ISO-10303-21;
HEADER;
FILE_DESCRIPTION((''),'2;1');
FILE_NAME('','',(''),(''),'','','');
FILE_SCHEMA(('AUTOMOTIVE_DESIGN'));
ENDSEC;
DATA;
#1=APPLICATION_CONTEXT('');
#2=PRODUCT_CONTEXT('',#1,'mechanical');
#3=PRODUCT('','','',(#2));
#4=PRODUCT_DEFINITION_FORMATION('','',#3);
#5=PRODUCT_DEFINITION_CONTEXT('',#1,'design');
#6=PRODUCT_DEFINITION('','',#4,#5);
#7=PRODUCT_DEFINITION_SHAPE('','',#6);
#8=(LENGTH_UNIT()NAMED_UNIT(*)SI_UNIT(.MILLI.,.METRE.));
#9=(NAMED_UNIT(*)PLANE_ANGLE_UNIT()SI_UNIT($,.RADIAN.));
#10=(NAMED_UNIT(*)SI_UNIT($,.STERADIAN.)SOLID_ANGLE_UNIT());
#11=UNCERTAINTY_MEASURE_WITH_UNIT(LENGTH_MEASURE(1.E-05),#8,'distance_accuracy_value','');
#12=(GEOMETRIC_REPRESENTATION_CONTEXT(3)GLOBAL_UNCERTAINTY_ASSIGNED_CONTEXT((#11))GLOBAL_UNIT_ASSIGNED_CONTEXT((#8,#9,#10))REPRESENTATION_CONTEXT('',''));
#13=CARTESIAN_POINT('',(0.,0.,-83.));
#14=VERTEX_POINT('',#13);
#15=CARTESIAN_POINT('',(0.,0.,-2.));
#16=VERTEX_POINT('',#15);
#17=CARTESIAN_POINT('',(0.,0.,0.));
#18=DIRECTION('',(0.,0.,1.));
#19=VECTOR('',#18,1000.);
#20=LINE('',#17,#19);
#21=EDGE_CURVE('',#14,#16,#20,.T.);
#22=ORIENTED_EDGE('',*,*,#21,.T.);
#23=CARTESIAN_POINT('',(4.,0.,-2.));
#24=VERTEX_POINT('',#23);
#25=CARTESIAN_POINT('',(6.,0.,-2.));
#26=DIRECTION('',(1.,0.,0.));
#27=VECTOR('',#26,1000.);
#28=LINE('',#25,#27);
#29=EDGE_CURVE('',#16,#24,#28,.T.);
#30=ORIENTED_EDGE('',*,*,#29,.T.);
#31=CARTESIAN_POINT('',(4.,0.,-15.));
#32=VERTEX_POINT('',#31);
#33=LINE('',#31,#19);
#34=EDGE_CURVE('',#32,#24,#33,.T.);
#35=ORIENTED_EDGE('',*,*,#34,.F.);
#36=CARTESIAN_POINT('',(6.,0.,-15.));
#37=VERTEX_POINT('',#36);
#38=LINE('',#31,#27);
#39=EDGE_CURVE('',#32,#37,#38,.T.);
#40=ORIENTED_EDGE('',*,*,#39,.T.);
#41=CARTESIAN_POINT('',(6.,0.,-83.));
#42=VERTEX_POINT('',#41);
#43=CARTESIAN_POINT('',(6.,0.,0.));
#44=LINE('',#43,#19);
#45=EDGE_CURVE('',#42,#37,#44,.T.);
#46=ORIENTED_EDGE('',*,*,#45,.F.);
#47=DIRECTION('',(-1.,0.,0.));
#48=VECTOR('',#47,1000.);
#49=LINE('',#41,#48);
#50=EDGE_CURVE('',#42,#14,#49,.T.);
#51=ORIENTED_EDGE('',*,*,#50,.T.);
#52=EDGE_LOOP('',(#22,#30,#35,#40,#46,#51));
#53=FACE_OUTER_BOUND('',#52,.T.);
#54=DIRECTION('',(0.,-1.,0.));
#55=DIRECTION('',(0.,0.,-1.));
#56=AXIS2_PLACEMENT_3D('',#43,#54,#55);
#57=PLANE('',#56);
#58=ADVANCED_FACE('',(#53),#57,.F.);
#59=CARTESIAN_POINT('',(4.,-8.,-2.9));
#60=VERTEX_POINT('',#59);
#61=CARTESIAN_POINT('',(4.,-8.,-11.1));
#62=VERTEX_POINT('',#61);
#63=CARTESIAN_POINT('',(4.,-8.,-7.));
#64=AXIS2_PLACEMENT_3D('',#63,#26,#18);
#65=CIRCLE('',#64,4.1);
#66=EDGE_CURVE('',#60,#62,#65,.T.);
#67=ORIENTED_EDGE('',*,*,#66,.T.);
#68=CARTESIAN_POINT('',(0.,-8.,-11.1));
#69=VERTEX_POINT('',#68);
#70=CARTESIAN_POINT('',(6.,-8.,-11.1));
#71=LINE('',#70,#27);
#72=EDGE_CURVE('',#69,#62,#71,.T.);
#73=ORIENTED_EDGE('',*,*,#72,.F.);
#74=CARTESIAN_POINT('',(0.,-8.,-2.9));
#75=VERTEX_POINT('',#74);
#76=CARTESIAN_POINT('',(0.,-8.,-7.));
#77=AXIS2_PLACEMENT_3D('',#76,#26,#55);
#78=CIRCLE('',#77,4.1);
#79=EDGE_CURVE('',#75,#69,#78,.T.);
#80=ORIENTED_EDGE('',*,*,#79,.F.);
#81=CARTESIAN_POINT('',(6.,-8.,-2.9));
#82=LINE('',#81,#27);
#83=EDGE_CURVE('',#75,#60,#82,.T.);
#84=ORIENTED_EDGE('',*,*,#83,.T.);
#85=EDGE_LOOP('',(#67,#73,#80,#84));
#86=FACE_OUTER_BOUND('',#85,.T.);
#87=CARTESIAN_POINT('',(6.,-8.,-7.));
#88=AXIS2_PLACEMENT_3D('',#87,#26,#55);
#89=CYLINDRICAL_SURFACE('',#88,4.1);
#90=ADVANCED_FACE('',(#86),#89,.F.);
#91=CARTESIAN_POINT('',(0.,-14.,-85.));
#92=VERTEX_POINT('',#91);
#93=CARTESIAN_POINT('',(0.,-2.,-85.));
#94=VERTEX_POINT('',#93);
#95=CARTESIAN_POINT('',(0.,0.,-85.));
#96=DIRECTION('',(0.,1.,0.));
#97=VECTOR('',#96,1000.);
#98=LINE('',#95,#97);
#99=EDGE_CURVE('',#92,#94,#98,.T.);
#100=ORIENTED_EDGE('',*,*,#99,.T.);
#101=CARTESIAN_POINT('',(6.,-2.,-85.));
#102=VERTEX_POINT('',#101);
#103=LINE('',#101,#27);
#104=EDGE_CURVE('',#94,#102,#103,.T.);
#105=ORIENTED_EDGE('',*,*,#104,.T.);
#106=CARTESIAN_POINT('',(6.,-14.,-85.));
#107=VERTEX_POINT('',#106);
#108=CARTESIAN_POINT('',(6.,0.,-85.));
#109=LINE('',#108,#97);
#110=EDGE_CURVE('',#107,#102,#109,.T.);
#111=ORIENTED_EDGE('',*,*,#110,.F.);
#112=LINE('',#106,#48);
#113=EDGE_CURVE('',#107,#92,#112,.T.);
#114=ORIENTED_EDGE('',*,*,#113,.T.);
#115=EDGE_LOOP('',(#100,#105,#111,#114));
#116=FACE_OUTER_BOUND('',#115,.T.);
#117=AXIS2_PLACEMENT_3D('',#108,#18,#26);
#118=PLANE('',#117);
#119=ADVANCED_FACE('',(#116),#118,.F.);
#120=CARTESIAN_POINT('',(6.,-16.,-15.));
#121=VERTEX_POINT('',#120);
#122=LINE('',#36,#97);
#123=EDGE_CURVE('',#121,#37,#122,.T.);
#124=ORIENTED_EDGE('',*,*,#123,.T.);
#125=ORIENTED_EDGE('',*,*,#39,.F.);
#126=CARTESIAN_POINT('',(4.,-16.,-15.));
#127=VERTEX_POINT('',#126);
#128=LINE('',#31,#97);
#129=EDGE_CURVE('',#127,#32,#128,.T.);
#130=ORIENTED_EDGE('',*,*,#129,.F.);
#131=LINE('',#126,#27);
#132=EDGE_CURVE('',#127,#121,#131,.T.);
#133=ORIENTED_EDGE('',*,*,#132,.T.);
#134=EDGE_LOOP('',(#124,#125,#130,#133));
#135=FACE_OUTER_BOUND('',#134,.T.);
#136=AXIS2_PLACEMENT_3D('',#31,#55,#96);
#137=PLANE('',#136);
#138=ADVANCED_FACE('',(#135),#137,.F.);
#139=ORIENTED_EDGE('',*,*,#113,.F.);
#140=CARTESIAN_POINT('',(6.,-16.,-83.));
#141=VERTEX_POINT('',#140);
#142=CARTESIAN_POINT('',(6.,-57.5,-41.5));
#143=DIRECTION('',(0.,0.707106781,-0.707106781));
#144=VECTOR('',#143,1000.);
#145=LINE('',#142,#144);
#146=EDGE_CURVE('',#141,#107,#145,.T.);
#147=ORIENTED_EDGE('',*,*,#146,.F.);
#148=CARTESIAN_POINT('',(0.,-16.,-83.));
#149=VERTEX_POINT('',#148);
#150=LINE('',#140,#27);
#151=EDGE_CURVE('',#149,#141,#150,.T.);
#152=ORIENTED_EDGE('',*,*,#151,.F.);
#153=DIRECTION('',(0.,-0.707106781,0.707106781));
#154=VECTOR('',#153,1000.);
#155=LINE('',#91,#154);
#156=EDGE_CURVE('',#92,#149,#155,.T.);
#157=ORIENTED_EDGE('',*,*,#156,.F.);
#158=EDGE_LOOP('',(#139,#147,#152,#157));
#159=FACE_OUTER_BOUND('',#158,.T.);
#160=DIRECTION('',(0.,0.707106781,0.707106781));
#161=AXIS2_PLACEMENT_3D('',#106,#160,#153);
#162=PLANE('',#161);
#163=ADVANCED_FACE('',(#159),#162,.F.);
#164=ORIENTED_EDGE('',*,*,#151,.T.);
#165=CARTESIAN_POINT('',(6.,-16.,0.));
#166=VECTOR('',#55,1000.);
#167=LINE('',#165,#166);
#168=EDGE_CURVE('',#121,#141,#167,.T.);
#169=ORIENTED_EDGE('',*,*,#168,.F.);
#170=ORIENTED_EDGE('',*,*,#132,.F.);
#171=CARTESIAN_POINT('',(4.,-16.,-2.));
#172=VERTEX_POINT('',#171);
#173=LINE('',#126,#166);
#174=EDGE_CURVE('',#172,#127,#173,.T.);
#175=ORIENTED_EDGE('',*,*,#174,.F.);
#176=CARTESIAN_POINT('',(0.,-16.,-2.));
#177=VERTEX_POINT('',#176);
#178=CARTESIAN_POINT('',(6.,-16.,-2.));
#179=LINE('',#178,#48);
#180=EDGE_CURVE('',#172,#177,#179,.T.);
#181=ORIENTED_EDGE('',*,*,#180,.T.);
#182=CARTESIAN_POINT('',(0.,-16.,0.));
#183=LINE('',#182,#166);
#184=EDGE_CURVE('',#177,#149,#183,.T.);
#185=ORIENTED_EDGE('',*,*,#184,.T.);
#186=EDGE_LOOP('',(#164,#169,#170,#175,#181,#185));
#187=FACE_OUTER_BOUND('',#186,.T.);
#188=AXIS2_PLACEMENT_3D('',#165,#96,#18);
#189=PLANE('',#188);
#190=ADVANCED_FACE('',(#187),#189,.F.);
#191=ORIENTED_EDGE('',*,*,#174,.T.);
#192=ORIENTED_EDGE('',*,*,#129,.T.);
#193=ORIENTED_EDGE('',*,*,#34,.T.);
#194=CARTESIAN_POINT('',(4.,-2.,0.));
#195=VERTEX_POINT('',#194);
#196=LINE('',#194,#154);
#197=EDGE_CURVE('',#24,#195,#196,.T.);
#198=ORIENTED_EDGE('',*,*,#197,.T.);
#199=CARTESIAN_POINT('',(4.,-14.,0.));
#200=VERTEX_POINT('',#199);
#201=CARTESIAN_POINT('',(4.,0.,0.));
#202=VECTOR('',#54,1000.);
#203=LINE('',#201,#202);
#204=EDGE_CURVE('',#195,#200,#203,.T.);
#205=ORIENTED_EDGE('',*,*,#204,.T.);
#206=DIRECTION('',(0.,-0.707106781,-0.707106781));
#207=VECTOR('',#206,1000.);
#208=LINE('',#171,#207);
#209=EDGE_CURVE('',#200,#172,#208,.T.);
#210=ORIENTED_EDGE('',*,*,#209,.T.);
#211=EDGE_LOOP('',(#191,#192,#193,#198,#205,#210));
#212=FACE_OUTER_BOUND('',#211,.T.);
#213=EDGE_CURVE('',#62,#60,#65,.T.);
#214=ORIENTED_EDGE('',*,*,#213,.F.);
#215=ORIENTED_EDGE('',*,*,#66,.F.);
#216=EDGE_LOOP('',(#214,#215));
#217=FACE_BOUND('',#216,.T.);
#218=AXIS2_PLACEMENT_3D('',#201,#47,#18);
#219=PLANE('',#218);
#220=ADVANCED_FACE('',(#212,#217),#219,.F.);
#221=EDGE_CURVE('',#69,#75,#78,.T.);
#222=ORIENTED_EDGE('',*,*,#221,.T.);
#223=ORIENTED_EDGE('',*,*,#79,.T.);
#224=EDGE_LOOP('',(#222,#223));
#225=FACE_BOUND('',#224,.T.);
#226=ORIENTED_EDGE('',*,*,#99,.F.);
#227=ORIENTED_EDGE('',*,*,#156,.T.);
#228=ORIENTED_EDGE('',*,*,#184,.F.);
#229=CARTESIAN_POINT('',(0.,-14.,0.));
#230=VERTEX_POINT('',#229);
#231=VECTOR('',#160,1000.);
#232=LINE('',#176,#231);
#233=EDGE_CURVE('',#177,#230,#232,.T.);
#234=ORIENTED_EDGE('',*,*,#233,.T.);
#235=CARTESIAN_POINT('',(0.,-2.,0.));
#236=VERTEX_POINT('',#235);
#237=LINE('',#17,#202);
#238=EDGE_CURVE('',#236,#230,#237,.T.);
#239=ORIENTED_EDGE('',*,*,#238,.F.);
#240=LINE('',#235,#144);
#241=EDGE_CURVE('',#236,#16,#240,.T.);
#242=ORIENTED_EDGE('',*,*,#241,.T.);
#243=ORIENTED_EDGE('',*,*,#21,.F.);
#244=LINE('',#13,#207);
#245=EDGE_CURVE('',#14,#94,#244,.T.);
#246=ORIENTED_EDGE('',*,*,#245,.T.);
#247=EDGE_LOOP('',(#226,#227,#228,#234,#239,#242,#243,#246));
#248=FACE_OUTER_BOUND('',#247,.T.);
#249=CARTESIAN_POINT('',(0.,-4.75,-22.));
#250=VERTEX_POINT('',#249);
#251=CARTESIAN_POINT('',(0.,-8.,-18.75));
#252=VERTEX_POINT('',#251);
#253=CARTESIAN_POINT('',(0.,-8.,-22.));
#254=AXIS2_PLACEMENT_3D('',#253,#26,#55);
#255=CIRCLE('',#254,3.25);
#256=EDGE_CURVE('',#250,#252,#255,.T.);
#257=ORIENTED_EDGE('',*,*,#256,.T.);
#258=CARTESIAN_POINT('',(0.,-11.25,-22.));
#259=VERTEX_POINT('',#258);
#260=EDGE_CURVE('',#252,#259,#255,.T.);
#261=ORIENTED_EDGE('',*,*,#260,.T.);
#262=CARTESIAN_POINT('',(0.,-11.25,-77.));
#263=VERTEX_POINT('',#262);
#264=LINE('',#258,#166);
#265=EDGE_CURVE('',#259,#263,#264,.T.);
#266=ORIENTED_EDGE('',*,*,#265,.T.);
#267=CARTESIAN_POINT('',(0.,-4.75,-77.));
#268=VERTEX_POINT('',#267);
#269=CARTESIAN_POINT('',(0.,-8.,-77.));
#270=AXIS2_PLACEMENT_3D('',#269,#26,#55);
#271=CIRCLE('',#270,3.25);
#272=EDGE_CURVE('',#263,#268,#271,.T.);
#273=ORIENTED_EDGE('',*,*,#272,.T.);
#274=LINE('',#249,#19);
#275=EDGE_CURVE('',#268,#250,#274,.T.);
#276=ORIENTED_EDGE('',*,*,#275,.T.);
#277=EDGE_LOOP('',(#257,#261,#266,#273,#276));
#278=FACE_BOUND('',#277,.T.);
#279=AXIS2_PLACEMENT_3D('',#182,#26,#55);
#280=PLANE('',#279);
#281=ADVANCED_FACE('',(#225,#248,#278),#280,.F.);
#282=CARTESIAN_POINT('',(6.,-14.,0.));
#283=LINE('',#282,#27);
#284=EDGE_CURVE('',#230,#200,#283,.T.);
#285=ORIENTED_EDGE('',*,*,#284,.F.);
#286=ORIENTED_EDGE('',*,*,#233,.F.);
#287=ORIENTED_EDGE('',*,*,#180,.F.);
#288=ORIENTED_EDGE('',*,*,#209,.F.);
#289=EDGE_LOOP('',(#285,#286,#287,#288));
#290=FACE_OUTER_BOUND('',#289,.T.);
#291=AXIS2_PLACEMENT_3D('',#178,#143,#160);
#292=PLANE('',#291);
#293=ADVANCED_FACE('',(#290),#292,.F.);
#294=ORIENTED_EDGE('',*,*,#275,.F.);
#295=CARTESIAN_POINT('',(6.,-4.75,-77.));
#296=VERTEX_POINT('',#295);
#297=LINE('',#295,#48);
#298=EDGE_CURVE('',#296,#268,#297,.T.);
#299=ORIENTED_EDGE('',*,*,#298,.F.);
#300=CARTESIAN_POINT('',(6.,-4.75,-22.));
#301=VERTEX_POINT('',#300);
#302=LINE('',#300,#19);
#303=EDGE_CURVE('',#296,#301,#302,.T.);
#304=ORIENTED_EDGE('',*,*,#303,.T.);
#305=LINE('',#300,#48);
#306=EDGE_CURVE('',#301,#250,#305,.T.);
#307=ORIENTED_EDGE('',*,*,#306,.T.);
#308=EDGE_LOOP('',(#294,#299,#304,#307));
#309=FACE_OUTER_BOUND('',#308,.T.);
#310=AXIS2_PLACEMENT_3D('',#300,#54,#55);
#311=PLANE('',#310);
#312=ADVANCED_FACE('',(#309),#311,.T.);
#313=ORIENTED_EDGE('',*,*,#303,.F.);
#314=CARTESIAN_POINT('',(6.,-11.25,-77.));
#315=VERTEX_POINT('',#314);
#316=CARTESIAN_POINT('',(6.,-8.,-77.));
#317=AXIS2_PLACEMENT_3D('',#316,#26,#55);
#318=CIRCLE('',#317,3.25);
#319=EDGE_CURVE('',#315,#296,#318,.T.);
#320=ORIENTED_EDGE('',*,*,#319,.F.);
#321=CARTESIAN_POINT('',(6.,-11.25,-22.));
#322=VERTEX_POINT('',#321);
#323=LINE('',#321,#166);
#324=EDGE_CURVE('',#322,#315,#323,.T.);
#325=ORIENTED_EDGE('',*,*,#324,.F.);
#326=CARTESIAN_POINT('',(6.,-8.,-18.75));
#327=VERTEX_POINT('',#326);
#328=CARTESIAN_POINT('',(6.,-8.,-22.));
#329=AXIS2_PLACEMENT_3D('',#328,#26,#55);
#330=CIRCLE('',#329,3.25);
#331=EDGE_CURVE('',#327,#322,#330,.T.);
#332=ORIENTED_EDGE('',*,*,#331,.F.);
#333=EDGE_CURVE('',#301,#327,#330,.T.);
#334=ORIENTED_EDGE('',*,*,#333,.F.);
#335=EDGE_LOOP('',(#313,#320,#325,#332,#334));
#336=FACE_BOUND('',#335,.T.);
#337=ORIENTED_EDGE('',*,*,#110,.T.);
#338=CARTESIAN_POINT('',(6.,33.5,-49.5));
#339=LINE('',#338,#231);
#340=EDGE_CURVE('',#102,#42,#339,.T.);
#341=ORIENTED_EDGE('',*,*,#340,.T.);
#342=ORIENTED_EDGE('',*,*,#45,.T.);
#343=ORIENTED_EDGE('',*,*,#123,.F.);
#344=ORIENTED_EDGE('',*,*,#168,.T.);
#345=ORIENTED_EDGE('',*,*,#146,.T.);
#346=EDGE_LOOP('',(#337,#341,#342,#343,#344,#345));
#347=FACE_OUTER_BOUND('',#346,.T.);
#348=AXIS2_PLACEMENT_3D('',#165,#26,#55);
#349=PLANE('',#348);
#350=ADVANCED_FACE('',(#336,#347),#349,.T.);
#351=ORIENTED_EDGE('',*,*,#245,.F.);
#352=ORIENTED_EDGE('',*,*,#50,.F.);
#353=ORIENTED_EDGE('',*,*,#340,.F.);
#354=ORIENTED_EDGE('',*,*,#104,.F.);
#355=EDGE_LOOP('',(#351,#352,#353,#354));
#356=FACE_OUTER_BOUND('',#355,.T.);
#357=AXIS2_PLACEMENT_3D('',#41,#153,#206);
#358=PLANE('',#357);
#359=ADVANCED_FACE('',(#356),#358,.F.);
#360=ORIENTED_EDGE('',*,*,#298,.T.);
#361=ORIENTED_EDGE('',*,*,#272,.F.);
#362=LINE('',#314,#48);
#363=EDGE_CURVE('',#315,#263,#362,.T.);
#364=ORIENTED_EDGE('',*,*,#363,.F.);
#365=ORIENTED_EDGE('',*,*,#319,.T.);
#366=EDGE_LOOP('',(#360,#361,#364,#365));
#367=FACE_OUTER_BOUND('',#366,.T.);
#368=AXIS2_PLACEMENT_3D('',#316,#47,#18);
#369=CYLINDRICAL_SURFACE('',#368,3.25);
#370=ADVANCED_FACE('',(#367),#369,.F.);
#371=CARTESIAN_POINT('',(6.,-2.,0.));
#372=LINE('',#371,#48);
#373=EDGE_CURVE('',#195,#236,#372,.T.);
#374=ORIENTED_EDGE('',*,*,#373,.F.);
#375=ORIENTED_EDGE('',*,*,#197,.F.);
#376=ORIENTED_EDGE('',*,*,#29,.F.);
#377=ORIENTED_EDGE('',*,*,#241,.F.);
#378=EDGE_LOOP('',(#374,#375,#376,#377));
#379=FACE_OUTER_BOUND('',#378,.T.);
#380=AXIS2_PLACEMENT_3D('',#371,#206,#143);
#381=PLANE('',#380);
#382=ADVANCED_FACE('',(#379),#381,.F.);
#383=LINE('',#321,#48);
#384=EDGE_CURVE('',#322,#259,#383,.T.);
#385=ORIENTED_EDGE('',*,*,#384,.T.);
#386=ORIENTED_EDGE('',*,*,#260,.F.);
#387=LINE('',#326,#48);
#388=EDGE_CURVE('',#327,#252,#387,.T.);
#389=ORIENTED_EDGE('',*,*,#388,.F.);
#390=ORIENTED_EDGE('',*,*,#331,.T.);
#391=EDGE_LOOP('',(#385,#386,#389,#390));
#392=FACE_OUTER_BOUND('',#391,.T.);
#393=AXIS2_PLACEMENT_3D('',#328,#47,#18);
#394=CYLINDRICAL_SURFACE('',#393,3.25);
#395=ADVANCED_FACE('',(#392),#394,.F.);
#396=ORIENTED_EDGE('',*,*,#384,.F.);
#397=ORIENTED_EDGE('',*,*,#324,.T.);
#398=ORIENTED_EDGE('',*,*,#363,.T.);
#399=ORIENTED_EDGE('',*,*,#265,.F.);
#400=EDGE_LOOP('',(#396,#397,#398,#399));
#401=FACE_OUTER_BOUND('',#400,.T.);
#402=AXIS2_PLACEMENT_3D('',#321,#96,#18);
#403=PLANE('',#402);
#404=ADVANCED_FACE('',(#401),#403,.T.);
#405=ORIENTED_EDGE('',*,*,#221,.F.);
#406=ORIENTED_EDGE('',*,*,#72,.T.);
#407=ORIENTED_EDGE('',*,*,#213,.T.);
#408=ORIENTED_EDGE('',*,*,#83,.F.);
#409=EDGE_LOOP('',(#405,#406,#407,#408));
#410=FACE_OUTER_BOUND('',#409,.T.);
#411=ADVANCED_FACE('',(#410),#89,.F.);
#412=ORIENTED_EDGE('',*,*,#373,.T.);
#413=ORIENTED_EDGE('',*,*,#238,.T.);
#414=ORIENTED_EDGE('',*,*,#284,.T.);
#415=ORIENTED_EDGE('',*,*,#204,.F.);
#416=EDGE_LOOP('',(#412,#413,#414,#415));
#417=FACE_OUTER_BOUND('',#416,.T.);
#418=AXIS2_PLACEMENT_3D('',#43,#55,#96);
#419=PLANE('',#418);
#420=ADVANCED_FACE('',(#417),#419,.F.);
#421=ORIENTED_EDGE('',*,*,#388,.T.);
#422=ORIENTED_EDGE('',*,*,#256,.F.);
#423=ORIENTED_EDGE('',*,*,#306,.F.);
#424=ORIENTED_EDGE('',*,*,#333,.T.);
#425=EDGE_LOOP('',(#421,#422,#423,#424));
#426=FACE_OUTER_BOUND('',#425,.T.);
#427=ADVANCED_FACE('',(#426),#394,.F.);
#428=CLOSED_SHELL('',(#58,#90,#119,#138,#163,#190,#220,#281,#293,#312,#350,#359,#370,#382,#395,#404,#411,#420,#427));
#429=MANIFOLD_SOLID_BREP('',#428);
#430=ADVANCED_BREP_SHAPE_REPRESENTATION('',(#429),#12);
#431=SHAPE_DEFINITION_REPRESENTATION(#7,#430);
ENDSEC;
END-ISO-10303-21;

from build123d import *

# Parameters (mm, degrees)
SKETCH1_W                  = 85
SKETCH1_H                  = 16
EXTRUDE1_DEPTH             = 6
F_8_2_8_2_DIAMETER_HOLE1_D = 8.2
CHAMFER1_SIZE              = 2
SKETCH5_W                  = 15
SKETCH5_H                  = 16
CUT_EXTRUDE1_DEPTH         = 2


with BuildPart() as part:
    # Sketch1 → Extrude1 (new body)
    with BuildSketch(Plane(origin=(0, 0, 0), x_dir=(0, 0, -1), z_dir=(1, 0, 0))):
        with Locations((42.5, -8)):
            Rectangle(SKETCH1_W, SKETCH1_H)
        with BuildLine():
            Line((22, -4.75), (77, -4.75))
            ThreePointArc((77, -4.75), (80.25, -8), (77, -11.25))
            Line((77, -11.25), (22, -11.25))
            ThreePointArc((22, -11.25), (18.75, -8), (22, -4.75))
        make_face(mode=Mode.SUBTRACT)
    extrude(amount=EXTRUDE1_DEPTH)

    # Ø8.2 (8.2) Diameter Hole1 (through all)
    with Locations(Plane(origin=(6, 0, 0), x_dir=(0, 0, -1), z_dir=(1, 0, 0))):
        with Locations((7, -8)):
            Hole(F_8_2_8_2_DIAMETER_HOLE1_D / 2)

    # Chamfer1
    chamfer1_edges = [part.edges().sort_by_distance(p)[0] for p in [
        (3, 0, 0),
        (3, 0, -85),
        (3, -16, -85),
        (3, -16, 0),
    ]]
    chamfer(chamfer1_edges, length=CHAMFER1_SIZE)

    # Sketch5 → Cut-Extrude1 (cut)
    with BuildSketch(Plane(origin=(6, 0, 0), x_dir=(0, 0, -1), z_dir=(1, 0, 0))):
        with Locations((7.5, -8)):
            Rectangle(SKETCH5_W, SKETCH5_H)
    extrude(amount=-CUT_EXTRUDE1_DEPTH, mode=Mode.SUBTRACT)


solid = part.part
